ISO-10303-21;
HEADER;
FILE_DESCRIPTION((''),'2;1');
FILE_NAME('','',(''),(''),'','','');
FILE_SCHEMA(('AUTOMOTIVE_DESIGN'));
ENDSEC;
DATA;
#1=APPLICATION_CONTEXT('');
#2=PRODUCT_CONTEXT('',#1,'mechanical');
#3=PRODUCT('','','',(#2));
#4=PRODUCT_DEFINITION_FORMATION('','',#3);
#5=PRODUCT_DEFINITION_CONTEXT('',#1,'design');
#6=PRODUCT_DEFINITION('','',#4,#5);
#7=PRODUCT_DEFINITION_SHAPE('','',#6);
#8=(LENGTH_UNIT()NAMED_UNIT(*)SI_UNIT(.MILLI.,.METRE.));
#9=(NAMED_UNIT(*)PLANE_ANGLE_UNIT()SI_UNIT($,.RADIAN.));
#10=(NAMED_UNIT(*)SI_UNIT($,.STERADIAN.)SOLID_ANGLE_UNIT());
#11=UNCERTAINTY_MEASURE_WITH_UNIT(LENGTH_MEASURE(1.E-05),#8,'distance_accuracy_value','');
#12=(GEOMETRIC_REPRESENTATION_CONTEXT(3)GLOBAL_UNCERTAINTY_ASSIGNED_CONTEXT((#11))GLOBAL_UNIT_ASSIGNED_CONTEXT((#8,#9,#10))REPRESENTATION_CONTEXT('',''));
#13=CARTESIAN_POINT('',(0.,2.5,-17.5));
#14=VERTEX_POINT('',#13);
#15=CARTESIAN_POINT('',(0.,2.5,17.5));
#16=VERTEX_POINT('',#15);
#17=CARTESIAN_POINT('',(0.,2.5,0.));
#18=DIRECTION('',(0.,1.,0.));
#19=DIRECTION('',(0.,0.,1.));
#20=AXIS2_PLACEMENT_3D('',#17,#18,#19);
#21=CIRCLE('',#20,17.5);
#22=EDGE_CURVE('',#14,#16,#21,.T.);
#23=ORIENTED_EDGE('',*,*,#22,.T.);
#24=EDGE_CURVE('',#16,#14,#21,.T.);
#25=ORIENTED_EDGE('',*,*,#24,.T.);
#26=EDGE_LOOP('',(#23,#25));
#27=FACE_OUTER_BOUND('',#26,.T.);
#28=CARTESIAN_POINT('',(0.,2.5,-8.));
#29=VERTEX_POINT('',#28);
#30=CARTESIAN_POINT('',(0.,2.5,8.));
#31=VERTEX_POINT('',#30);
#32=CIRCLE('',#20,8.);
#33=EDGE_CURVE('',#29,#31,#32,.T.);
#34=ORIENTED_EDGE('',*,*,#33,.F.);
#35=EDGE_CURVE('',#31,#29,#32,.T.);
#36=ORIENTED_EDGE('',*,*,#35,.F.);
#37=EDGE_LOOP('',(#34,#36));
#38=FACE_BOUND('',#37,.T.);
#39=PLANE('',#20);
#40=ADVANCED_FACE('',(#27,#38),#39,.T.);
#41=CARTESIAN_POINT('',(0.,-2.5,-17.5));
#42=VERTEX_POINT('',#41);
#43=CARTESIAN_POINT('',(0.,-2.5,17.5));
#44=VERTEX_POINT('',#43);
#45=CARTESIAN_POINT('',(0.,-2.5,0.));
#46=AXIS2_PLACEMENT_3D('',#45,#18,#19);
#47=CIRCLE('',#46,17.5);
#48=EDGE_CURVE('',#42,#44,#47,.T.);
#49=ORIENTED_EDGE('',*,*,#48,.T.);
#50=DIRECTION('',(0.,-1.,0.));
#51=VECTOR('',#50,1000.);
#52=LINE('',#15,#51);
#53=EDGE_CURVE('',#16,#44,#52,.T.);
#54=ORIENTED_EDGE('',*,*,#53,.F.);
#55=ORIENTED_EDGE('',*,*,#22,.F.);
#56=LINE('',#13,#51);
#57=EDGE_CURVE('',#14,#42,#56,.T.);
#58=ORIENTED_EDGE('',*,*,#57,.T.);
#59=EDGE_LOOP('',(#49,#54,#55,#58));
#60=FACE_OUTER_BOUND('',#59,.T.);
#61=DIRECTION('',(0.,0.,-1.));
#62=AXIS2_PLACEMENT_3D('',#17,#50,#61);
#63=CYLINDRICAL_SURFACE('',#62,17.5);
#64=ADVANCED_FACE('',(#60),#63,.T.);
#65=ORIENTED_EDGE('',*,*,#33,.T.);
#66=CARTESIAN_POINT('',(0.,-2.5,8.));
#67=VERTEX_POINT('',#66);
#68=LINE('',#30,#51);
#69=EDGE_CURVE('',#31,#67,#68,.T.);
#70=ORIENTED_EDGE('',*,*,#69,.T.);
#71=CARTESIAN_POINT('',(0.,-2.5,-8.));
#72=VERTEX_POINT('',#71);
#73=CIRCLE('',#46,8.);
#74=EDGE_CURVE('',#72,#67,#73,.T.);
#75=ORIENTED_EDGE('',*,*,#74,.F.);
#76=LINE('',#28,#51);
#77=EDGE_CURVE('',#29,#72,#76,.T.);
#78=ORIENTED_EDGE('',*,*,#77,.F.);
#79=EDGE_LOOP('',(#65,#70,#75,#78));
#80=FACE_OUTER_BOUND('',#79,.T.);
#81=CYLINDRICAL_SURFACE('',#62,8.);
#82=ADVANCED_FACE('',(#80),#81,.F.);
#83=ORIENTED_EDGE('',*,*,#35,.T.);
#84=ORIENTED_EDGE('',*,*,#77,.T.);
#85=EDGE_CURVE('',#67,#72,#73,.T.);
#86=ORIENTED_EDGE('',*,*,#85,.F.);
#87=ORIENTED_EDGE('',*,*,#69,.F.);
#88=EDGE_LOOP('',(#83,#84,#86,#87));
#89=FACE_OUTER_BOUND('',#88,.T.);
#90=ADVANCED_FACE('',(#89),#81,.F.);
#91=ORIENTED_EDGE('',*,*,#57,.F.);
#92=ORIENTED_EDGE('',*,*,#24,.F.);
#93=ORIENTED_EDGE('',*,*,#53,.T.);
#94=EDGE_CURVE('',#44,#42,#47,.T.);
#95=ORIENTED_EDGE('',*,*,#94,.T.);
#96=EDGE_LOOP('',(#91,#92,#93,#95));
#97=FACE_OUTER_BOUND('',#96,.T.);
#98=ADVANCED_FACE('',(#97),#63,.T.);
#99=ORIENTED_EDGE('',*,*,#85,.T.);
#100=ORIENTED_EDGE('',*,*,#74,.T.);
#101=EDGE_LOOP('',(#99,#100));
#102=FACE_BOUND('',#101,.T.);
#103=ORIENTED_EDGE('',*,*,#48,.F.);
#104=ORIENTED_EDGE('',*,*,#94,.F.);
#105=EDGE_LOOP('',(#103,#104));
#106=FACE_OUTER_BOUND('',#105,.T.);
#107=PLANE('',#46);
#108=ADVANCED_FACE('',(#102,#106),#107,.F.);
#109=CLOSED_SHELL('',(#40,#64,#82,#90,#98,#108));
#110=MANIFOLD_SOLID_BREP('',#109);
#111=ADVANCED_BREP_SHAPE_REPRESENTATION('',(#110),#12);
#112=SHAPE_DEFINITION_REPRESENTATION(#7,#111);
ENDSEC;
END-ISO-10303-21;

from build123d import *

# Parameters (mm, degrees)
WASHER_PROFILE_35_16_R   = 17.5
WASHER_PROFILE_35_16_R_2 = 8
WASHER_BODY_5MM_DEPTH    = 2.5


with BuildPart() as part:
    # Washer Profile Ø35-Ø16 → Washer Body 5mm (new, symmetric)
    with BuildSketch(Plane(origin=(0, 0, 0), x_dir=(1, 0, 0), z_dir=(0, 1, 0))):
        with Locations(Location((0, 0, 0), (0, 0, 270))):
            Circle(WASHER_PROFILE_35_16_R)
        with Locations(Location((0, 0, 0), (0, 0, 270))):
            Circle(WASHER_PROFILE_35_16_R_2, mode=Mode.SUBTRACT)
    extrude(amount=WASHER_BODY_5MM_DEPTH, both=True)


solid = part.part
